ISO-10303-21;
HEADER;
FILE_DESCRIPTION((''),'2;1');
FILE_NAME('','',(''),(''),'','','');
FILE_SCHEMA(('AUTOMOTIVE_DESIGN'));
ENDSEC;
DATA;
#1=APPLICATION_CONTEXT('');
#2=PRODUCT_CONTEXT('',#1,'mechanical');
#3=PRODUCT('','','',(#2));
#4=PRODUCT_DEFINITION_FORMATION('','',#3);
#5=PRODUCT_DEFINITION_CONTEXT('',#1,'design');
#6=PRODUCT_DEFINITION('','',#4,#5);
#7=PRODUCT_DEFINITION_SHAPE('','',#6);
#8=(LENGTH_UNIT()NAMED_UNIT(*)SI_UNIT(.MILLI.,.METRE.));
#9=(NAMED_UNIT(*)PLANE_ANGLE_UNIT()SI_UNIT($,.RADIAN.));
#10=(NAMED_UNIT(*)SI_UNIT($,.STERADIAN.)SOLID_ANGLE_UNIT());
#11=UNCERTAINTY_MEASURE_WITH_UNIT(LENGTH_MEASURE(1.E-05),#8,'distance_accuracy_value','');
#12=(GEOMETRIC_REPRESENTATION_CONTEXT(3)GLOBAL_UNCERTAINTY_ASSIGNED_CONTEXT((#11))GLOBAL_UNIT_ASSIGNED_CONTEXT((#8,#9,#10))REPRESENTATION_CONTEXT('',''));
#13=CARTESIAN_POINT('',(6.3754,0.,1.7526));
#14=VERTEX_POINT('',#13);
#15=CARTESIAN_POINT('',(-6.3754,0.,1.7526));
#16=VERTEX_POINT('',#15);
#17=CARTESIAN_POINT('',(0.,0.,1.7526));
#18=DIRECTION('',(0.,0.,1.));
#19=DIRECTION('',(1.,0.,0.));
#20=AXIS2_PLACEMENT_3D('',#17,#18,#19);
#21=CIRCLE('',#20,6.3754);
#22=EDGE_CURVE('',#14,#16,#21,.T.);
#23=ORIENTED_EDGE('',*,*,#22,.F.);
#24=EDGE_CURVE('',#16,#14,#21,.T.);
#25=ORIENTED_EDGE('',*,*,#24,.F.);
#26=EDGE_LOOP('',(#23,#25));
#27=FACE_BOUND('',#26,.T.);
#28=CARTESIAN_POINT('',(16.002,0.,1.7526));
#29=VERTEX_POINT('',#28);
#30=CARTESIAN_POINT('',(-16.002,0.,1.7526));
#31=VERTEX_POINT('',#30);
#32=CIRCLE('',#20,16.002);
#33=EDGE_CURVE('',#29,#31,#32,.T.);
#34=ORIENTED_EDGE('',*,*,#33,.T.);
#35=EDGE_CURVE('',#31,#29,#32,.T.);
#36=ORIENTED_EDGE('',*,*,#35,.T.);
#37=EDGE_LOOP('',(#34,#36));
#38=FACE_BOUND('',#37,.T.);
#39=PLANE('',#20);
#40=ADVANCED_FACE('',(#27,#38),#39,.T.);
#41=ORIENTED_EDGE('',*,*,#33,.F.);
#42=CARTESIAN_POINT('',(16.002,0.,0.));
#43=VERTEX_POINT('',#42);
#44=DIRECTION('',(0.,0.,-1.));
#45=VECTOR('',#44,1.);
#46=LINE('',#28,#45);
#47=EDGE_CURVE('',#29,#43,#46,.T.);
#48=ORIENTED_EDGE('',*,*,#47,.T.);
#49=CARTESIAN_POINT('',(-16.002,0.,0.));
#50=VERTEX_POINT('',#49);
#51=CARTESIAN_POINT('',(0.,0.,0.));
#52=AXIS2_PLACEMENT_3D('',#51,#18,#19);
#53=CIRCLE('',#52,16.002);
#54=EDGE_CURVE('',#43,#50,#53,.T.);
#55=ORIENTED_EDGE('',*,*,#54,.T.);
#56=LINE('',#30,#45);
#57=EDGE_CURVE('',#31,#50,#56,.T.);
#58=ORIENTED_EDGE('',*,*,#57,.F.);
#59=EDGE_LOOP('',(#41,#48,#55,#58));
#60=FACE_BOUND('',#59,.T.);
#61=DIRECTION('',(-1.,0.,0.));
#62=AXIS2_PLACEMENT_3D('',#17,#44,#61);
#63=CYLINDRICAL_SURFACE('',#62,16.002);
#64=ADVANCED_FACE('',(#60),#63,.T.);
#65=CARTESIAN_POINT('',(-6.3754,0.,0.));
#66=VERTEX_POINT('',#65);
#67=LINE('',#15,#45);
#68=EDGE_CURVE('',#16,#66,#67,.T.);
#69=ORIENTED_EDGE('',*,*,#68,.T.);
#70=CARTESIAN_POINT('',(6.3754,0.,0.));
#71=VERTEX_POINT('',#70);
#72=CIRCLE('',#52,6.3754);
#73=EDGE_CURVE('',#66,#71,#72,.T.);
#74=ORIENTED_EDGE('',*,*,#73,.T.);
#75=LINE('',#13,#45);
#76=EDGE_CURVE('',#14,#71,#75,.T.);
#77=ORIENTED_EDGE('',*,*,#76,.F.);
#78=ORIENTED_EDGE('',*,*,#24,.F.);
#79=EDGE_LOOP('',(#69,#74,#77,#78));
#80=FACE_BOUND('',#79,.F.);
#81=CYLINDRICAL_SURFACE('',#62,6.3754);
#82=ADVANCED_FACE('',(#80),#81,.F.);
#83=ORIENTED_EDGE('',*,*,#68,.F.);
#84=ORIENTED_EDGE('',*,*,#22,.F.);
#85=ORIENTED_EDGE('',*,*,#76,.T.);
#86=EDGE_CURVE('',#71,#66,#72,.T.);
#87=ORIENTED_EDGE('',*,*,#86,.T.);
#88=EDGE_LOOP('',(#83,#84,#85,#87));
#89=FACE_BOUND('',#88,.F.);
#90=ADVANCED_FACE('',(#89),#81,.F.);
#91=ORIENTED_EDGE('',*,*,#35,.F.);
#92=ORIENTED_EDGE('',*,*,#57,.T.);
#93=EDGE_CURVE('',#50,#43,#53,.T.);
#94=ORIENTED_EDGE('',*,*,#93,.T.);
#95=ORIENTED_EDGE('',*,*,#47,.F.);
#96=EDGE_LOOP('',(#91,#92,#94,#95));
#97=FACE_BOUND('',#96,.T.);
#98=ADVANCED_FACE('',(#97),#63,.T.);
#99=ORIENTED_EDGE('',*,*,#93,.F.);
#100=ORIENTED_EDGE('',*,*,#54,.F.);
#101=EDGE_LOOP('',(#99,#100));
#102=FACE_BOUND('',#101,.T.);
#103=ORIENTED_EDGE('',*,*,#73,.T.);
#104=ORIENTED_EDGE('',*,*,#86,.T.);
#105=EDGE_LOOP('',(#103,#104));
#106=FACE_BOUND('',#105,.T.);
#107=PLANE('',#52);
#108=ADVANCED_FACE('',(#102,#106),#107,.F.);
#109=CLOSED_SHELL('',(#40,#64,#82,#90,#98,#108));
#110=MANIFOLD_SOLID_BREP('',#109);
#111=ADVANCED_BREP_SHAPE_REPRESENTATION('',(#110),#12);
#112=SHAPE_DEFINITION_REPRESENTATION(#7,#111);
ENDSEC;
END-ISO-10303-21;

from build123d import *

# Parameters (mm, degrees)
SKETCH1_R           = 16.002
SKETCH1_R_2         = 6.3754
BOSS_EXTRUDE1_DEPTH = 1.7526


with BuildPart() as part:
    # Sketch1 → Boss-Extrude1 (new body)
    with BuildSketch(Plane.XY):
        Circle(SKETCH1_R)
        Circle(SKETCH1_R_2, mode=Mode.SUBTRACT)
    extrude(amount=BOSS_EXTRUDE1_DEPTH)


solid = part.part
